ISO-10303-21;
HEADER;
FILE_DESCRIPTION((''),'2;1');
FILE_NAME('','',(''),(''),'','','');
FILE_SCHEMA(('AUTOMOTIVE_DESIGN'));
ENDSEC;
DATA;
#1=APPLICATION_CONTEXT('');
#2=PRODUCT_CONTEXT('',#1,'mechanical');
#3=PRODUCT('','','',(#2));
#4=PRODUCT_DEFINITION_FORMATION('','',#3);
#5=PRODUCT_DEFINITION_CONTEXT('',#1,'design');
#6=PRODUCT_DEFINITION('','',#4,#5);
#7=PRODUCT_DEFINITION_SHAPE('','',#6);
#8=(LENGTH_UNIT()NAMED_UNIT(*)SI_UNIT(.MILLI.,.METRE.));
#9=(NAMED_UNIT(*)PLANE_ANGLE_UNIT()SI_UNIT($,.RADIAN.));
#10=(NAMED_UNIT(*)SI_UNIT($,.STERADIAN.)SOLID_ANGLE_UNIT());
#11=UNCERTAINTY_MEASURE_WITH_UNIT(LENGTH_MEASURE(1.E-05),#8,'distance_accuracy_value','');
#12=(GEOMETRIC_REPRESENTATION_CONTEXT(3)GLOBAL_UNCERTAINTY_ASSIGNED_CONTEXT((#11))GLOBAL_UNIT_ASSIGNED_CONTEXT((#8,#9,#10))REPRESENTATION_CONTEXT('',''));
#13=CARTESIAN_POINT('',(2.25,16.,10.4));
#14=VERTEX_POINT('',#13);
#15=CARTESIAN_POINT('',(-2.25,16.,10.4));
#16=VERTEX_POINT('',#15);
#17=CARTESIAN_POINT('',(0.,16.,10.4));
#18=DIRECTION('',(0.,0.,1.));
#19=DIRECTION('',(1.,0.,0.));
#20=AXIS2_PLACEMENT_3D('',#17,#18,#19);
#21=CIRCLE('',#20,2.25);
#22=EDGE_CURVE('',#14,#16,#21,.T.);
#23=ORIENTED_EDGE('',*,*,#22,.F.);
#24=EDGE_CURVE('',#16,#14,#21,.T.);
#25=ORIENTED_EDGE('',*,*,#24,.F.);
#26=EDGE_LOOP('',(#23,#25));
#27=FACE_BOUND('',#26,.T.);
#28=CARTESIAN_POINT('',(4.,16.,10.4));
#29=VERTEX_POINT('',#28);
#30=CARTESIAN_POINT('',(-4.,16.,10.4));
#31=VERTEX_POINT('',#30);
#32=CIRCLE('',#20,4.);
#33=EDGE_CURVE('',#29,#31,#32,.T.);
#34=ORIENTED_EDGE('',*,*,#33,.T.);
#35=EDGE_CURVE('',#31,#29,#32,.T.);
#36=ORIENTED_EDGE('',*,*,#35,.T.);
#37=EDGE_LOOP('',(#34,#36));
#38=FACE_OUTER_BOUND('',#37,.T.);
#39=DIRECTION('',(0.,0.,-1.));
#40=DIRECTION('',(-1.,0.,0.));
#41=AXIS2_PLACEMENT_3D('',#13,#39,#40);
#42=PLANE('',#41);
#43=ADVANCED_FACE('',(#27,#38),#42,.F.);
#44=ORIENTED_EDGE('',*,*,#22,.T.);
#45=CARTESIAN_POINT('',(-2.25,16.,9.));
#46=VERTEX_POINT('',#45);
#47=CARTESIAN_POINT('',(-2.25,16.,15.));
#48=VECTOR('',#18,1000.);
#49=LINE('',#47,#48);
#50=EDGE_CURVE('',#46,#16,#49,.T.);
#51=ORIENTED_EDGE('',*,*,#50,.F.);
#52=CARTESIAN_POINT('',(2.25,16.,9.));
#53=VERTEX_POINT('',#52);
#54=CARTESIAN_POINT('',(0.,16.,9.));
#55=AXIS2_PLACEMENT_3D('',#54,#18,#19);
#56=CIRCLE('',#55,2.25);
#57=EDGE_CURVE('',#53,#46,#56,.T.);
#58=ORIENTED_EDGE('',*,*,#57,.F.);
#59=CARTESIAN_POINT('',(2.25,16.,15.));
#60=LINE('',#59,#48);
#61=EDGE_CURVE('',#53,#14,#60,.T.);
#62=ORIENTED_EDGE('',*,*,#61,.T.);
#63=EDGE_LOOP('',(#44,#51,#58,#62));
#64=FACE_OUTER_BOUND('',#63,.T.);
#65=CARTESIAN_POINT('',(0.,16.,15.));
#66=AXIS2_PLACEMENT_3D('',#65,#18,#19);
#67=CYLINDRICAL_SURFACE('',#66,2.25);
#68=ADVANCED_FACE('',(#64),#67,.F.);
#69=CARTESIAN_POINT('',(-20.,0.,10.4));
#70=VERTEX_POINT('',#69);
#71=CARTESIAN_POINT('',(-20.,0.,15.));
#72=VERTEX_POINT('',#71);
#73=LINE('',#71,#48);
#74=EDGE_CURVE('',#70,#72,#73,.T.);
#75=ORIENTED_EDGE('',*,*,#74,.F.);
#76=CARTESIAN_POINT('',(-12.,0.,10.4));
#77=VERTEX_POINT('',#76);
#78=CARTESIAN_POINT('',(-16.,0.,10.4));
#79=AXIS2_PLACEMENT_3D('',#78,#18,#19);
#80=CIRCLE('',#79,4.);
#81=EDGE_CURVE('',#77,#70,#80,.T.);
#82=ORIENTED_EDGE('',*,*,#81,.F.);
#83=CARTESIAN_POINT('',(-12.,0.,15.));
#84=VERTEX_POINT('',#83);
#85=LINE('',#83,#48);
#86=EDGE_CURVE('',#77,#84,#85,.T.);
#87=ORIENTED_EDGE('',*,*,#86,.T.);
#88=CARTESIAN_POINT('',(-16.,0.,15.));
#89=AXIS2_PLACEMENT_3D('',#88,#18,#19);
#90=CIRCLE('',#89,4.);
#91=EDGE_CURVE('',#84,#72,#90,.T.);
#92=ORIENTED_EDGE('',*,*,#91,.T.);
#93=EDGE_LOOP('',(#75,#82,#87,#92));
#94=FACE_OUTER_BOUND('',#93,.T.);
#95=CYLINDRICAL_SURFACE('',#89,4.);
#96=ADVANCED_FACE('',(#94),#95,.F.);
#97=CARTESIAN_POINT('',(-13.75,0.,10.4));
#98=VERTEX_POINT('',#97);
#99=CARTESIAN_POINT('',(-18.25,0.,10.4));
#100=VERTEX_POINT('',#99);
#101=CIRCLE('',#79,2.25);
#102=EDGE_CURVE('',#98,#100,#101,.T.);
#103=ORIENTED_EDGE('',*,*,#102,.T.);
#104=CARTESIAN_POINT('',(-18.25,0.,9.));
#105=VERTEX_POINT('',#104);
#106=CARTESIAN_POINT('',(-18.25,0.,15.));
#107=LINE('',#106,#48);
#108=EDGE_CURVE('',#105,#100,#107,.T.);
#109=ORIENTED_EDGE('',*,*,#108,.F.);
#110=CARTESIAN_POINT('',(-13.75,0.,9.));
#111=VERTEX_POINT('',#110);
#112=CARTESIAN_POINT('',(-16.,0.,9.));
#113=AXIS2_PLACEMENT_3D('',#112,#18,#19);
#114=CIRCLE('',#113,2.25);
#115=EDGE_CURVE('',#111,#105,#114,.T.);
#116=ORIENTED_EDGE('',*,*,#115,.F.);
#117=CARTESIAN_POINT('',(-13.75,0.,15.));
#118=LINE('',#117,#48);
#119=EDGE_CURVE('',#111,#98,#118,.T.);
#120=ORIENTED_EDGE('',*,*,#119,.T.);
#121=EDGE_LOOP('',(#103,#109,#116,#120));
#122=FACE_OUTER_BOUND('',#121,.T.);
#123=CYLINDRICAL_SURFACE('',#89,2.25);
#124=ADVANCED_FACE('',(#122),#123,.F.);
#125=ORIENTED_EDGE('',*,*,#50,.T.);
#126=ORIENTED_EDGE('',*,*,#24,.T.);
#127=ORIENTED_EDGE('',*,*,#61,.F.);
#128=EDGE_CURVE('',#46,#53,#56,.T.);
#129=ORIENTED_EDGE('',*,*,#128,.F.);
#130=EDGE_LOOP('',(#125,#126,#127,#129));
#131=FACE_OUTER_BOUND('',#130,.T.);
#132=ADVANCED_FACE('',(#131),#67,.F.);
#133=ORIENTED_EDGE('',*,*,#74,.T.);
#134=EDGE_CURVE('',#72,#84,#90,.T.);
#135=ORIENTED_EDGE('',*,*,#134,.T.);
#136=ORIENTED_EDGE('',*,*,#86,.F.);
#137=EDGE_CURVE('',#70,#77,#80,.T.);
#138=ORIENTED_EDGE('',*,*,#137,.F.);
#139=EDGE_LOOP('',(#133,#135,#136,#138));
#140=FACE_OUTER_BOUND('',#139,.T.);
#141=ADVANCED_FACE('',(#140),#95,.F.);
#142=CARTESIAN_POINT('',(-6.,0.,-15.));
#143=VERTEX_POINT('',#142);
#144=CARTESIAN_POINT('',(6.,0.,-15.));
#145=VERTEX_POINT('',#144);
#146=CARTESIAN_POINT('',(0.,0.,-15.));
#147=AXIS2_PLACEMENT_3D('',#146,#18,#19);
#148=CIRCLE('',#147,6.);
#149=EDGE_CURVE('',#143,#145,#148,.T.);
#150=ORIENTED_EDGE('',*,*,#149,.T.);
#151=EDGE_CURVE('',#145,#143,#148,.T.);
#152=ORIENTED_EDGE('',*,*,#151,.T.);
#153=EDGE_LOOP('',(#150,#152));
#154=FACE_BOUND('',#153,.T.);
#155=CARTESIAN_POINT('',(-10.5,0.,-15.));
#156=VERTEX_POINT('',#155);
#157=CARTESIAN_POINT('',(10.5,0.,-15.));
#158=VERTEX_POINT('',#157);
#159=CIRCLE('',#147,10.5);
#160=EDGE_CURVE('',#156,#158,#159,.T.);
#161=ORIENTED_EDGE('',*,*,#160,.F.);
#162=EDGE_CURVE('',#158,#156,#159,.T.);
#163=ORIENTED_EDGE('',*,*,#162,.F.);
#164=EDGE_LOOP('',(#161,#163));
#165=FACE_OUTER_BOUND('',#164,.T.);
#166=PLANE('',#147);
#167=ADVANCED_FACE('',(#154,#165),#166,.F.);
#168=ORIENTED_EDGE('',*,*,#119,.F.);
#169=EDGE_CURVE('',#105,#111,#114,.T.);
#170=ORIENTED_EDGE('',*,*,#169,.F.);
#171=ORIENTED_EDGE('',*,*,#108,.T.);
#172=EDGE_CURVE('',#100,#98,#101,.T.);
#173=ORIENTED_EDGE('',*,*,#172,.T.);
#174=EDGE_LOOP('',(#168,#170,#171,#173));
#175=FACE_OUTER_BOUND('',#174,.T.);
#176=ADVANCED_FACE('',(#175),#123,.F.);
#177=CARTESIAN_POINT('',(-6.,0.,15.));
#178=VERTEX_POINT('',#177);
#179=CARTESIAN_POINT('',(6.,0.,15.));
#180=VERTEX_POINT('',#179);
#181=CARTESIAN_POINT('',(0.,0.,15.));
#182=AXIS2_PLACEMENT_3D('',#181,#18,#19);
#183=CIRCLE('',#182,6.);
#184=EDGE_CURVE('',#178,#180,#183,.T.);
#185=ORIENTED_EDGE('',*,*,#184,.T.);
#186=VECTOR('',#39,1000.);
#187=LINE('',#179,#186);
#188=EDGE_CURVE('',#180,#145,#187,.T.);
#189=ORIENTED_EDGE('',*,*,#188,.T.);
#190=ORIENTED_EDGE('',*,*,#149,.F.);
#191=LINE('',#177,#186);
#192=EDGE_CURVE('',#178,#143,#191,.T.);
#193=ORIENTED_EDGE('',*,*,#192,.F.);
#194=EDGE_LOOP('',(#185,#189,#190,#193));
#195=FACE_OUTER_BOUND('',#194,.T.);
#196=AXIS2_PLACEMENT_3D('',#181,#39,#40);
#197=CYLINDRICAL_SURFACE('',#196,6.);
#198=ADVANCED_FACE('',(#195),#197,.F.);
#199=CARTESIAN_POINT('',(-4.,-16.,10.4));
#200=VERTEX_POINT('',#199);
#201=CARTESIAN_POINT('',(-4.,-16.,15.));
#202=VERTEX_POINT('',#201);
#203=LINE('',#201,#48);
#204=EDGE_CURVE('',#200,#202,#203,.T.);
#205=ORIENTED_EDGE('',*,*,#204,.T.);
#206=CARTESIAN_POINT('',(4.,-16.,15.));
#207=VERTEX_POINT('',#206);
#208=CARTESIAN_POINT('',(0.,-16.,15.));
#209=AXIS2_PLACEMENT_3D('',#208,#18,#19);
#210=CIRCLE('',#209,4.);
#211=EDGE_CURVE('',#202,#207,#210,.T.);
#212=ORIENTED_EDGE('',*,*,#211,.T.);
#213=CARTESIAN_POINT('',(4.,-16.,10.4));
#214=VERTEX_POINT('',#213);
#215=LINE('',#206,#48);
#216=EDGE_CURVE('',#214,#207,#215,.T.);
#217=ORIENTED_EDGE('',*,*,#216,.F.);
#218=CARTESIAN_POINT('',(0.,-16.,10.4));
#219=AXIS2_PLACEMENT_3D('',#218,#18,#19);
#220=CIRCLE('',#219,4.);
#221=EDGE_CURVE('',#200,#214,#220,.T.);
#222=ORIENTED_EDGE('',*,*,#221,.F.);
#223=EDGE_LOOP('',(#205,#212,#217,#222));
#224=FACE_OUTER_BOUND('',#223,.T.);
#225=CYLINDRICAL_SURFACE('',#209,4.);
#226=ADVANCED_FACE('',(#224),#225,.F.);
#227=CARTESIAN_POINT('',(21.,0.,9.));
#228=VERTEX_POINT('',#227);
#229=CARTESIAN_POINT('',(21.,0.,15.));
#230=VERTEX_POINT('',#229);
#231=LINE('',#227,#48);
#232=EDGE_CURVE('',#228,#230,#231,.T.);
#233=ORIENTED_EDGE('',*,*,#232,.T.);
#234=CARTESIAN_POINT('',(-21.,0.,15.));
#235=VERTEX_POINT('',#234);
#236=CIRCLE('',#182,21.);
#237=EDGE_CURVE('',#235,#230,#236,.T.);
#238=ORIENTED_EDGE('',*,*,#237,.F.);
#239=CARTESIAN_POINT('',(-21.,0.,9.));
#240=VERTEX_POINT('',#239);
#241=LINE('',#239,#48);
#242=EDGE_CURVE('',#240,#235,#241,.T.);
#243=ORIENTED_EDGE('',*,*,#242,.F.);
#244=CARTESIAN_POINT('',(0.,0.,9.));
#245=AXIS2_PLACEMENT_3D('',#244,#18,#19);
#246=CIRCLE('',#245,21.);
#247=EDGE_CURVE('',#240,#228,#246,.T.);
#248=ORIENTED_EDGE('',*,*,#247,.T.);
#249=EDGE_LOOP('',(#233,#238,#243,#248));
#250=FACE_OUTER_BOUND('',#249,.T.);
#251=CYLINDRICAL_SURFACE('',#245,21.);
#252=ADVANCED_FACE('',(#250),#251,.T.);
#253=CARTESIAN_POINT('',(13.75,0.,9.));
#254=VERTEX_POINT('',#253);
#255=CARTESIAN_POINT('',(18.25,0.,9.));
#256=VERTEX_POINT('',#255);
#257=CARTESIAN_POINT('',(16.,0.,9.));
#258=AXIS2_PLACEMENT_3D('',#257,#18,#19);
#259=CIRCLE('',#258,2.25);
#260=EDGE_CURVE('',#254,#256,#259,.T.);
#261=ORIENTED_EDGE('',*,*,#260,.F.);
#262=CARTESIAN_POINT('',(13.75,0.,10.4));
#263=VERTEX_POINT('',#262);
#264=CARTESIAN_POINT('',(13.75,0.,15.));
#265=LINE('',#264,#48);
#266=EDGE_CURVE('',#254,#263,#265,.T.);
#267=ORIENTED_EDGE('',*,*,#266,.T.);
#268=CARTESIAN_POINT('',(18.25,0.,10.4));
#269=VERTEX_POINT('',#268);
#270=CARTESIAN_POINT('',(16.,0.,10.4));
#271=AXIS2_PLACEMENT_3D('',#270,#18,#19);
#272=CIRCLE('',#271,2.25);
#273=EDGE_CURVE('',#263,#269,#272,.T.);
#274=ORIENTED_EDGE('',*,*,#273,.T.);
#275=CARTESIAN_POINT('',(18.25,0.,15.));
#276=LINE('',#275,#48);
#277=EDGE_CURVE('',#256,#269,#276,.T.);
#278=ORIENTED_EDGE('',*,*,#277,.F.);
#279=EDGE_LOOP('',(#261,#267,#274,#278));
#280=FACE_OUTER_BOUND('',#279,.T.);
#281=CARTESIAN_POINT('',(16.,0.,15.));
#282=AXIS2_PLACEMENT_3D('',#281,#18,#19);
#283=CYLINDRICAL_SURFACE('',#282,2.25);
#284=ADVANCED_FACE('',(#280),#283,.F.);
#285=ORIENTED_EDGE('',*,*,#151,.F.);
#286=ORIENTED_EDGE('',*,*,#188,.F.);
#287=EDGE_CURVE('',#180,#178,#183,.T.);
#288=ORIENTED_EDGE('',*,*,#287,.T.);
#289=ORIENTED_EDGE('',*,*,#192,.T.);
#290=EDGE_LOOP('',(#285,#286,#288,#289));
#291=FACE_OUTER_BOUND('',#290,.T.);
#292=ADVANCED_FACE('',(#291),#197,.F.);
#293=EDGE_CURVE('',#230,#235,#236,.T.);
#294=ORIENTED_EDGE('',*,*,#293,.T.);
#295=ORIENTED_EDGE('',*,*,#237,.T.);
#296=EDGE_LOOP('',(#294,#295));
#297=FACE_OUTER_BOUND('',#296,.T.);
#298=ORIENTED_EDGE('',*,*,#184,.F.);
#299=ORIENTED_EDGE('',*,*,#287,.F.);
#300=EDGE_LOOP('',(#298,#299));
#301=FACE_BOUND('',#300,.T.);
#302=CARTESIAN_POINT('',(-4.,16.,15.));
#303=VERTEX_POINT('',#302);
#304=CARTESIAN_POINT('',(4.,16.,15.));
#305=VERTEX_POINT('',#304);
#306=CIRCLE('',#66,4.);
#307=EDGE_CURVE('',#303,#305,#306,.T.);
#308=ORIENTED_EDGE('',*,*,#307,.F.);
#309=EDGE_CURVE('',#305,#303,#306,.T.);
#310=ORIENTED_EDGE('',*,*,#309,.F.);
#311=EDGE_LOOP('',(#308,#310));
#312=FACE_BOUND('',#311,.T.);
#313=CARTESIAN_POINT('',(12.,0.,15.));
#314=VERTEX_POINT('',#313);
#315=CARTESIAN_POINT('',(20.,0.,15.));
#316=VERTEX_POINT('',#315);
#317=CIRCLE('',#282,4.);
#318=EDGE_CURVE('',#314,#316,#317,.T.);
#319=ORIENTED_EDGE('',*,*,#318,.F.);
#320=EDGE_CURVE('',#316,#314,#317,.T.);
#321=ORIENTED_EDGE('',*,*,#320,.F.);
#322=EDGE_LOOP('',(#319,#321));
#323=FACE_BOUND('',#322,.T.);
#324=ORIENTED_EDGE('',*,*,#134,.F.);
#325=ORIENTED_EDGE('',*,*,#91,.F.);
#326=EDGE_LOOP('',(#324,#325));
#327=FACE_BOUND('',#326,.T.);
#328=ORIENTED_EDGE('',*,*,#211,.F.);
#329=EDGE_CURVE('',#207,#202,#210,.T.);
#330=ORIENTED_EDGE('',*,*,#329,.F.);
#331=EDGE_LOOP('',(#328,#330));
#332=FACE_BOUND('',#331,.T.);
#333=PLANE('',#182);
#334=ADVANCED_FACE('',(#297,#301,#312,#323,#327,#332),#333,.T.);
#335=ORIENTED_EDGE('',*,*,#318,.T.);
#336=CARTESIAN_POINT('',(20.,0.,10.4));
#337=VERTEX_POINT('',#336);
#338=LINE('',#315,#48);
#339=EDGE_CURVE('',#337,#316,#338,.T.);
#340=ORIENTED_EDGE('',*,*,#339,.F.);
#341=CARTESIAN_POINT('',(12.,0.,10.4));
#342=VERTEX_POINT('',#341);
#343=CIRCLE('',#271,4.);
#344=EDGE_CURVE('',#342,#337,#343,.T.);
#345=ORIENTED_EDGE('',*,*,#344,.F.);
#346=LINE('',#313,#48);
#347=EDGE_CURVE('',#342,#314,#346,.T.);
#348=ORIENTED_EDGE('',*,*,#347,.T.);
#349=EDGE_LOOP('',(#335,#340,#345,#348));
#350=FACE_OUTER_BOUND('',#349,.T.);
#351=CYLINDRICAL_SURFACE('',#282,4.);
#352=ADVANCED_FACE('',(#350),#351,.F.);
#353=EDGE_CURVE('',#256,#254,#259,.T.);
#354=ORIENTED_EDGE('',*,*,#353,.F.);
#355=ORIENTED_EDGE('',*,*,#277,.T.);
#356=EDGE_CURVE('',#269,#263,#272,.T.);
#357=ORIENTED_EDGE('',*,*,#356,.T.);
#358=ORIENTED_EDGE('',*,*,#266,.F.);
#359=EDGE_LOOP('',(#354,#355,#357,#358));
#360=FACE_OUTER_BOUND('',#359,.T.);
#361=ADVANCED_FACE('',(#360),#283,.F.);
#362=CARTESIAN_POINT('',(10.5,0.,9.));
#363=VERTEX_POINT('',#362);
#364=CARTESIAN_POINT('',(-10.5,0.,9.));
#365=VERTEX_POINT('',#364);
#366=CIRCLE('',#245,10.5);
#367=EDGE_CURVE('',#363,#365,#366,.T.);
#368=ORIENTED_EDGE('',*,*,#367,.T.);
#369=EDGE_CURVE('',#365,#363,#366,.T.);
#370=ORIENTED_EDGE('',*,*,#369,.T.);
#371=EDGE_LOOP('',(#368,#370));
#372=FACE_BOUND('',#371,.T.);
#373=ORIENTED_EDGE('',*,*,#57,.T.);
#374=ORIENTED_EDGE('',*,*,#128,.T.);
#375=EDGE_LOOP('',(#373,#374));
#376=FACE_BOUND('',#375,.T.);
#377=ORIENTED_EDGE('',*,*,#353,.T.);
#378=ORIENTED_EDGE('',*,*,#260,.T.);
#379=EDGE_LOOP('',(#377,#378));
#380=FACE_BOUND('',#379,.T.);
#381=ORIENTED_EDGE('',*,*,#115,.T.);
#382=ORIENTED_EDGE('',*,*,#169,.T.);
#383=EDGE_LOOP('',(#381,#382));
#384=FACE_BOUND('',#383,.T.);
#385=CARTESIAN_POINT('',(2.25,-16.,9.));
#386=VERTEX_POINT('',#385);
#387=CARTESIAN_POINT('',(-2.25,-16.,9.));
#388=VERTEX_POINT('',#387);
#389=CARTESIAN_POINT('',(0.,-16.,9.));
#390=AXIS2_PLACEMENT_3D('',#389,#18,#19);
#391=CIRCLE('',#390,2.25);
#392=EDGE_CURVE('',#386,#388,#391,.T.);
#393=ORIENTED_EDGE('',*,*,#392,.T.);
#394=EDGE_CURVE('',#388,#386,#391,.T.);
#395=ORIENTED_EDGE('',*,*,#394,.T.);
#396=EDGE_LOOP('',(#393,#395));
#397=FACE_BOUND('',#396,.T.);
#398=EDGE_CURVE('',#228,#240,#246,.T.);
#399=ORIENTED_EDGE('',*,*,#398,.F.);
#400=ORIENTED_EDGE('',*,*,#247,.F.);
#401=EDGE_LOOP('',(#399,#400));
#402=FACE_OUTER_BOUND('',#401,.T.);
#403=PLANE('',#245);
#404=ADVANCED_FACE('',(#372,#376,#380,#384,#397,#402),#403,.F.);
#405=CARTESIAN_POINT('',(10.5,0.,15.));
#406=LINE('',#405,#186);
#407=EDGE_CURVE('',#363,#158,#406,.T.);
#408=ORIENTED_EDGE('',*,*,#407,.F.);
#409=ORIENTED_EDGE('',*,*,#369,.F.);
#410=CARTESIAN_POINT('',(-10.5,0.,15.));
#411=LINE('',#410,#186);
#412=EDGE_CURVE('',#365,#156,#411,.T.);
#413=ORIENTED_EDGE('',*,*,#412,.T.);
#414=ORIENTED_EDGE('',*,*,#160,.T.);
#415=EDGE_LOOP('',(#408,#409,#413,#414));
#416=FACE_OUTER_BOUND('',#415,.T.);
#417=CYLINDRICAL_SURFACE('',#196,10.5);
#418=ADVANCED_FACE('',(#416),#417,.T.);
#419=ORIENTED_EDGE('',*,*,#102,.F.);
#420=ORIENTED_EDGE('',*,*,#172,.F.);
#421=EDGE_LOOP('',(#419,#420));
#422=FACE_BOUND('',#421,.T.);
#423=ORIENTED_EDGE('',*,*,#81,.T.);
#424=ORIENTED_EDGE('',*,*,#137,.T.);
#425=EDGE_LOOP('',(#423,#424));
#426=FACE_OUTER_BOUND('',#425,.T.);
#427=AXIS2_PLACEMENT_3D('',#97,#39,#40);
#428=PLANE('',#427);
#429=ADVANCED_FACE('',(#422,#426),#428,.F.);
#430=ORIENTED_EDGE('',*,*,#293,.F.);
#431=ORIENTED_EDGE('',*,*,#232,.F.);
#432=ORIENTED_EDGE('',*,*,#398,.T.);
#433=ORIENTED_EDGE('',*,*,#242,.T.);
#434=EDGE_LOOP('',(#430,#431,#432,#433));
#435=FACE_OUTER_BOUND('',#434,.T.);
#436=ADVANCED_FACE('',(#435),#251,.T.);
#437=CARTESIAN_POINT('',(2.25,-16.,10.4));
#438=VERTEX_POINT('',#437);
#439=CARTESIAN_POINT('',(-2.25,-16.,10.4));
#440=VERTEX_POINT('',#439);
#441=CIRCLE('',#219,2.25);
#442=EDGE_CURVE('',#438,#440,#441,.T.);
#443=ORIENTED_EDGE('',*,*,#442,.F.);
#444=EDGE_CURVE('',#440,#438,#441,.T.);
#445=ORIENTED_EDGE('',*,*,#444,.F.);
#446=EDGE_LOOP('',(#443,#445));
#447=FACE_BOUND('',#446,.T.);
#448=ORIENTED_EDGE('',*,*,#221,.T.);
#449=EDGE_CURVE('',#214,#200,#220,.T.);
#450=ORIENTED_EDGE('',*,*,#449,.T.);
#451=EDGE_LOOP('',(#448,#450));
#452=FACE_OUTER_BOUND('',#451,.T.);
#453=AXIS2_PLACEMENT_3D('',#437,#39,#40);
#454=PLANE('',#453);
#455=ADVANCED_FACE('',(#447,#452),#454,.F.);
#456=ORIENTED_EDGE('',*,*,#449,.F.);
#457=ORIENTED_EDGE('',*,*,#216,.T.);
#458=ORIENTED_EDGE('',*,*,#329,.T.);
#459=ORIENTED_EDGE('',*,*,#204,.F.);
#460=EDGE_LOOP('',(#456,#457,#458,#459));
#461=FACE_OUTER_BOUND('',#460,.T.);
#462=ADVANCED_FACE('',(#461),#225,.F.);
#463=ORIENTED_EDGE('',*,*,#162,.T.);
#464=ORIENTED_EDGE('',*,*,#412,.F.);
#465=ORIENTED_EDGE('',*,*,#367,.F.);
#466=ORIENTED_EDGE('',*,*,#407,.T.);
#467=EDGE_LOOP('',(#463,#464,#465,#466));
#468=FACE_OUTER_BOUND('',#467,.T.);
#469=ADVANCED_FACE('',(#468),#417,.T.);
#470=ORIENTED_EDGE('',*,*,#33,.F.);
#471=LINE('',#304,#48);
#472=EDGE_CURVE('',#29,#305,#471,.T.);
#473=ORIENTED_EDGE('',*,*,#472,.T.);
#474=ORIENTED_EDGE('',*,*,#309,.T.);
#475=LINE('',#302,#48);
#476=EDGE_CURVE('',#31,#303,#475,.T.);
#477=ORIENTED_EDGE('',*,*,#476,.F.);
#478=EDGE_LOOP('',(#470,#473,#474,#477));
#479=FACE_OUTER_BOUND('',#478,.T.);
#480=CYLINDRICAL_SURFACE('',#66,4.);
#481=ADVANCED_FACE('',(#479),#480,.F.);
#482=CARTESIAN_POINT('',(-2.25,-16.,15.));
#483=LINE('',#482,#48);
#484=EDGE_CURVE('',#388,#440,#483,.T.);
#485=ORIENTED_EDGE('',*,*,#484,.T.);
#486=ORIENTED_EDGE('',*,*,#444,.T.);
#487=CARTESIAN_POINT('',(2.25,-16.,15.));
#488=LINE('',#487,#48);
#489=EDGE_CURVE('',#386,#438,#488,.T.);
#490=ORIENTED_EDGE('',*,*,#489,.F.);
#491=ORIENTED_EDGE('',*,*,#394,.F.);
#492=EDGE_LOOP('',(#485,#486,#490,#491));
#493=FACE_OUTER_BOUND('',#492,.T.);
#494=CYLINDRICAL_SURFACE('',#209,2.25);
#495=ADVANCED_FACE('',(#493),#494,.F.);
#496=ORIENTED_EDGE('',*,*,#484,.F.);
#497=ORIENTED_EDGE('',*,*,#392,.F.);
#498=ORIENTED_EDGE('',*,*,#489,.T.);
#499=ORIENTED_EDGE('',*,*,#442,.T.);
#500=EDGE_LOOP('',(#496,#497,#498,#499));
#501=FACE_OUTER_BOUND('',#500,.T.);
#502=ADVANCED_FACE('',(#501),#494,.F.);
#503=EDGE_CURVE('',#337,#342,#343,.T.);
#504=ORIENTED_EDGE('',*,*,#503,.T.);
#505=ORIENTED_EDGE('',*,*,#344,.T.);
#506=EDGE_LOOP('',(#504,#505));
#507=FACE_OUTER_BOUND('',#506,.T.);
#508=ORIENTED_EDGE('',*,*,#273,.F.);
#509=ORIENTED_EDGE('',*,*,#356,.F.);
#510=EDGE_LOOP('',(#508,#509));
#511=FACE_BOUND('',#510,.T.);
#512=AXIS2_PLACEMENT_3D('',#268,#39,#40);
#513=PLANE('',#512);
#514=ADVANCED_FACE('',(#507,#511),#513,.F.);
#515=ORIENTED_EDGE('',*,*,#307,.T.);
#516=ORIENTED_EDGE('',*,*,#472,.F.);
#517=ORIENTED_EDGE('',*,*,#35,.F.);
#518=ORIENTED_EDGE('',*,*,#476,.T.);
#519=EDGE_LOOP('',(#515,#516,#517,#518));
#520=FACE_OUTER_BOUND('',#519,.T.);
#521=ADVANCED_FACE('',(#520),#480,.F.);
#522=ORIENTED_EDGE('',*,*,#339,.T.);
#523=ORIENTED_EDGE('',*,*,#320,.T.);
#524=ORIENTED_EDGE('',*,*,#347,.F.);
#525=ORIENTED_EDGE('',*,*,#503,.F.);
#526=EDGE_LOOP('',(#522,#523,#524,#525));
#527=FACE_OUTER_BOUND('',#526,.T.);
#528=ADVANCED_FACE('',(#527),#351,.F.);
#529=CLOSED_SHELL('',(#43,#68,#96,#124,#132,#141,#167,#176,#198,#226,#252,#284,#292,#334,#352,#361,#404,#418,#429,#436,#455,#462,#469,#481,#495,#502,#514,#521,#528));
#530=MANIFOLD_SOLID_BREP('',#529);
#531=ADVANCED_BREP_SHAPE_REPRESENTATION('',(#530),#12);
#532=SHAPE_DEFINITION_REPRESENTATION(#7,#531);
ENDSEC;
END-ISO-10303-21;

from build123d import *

# Parameters (mm, degrees)
SKETCH_1_R                = 10.5
SKETCH_1_R_2              = 6
EXTRUDE_1_DEPTH           = 15
SKETCH_2_R                = 21
SKETCH_2_R_2              = 10.5
EXTRUDE_2_DEPTH           = 6
HOLE_WIZARD_1_D           = 4.5
HOLE_WIZARD_1_DEPTH       = 11.5
HOLE_WIZARD_1_CBORE_D     = 8
HOLE_WIZARD_1_CBORE_DEPTH = 4.6
HOLE_WIZARD_1_TIP         = 1.351936393


with BuildPart() as part:
    # 草图1 → 凸台-拉伸1 (new, symmetric)
    with BuildSketch(Plane.XY):
        Circle(SKETCH_1_R)
        Circle(SKETCH_1_R_2, mode=Mode.SUBTRACT)
    extrude(amount=EXTRUDE_1_DEPTH, both=True)

    # 草图2 → 凸台-拉伸2 (add)
    with BuildSketch(Plane.XY.offset(15)):
        Circle(SKETCH_2_R)
        Circle(SKETCH_2_R_2, mode=Mode.SUBTRACT)
    extrude(amount=-EXTRUDE_2_DEPTH)

    # 打孔尺寸(%根据)内六角圆柱头螺钉的类型1
    with Locations(Plane.XY.offset(15)):
        with Locations((0, 16), (16, 0), (0, -16), (-16, 0)):
            CounterBoreHole(HOLE_WIZARD_1_D / 2, HOLE_WIZARD_1_CBORE_D / 2, HOLE_WIZARD_1_CBORE_DEPTH, depth=HOLE_WIZARD_1_DEPTH)
            with Locations((0, 0, -(HOLE_WIZARD_1_DEPTH + HOLE_WIZARD_1_TIP / 2))):  # 118° drill point
                Cone(0, HOLE_WIZARD_1_D / 2, HOLE_WIZARD_1_TIP, mode=Mode.SUBTRACT)


solid = part.part
